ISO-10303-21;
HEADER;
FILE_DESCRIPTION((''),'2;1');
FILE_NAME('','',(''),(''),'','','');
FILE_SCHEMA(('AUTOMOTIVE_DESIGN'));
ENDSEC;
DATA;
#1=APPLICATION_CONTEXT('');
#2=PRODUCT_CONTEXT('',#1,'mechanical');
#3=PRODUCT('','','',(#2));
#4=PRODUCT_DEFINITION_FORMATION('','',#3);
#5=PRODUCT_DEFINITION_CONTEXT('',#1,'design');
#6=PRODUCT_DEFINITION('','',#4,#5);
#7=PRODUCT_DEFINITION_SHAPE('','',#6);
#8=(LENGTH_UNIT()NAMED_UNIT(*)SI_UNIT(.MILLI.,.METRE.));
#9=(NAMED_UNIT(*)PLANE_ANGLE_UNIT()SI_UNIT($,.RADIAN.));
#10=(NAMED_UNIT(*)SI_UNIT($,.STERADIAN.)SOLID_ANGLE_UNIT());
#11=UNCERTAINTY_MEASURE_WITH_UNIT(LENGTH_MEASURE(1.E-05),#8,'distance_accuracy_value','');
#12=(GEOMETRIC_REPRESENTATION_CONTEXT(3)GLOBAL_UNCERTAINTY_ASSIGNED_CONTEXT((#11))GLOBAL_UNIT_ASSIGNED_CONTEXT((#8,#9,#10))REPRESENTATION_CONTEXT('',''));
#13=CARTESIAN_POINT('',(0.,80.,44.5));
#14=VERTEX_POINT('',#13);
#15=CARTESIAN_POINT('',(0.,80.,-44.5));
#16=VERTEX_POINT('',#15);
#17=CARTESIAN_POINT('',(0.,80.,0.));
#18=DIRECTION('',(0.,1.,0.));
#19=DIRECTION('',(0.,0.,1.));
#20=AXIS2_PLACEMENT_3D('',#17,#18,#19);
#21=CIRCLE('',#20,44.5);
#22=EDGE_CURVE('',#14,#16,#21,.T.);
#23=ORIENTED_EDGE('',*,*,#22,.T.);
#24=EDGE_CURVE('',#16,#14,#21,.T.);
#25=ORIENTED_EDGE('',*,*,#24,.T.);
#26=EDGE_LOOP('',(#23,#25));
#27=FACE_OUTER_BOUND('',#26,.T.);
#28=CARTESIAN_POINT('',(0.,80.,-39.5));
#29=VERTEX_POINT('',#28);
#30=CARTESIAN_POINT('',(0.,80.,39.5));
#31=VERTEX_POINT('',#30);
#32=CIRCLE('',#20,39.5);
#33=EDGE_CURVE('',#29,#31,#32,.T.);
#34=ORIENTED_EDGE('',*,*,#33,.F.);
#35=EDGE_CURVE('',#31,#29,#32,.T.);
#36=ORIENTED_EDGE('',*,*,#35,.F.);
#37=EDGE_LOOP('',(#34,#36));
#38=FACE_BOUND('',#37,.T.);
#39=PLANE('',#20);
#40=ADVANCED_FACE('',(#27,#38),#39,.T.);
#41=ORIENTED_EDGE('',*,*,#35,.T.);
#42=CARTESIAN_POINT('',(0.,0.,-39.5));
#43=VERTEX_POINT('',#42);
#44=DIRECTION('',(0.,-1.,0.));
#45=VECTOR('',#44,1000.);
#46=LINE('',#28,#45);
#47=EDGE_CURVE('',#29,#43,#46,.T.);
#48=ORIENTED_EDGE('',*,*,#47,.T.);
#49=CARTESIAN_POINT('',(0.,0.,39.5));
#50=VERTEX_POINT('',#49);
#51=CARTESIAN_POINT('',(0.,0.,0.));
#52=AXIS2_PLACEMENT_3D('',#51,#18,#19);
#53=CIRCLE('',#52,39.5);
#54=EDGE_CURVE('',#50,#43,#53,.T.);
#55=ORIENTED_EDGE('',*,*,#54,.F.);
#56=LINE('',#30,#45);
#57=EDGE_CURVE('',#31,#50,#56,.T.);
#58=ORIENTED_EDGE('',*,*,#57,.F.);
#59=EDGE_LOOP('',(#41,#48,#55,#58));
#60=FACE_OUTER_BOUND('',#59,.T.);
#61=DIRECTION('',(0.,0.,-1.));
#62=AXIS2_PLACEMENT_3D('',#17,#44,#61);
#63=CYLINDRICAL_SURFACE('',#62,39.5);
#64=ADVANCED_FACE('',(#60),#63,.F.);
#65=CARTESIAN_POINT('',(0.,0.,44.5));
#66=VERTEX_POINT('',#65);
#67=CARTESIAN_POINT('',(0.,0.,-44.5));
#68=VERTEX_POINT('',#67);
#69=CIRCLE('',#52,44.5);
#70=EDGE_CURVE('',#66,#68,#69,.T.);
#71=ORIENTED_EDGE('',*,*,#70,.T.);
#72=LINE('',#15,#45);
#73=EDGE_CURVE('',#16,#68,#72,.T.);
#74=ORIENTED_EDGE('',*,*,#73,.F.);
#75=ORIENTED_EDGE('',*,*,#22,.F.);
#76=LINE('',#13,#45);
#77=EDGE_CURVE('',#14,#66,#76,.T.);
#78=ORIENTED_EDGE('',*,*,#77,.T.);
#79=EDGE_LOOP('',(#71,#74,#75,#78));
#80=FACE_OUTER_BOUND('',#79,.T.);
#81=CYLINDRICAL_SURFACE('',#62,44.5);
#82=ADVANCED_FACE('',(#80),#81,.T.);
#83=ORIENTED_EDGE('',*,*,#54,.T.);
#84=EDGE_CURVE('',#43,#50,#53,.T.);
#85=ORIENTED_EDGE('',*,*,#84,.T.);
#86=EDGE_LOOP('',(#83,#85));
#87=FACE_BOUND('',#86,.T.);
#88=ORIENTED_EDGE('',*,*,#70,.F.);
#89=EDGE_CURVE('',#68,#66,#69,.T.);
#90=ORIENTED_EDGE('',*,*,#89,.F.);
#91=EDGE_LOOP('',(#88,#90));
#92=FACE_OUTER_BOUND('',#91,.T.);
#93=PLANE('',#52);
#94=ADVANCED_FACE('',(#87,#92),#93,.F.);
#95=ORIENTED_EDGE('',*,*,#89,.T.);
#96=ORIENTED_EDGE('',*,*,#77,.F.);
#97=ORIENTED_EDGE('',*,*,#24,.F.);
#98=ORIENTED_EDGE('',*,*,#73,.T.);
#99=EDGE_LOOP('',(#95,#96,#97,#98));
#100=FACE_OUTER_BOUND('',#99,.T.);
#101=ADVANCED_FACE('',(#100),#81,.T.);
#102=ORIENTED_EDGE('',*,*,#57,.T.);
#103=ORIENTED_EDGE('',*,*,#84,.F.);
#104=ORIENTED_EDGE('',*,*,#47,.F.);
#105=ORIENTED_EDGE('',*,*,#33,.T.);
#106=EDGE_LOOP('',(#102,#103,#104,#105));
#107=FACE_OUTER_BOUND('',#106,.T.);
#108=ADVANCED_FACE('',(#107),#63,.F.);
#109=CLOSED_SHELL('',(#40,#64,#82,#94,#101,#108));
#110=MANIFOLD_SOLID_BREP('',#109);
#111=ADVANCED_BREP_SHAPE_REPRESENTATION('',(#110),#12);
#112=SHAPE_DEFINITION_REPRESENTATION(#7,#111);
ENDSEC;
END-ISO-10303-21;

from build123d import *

# Parameters (mm, degrees)
SKETCH1_R           = 44.5
SKETCH1_R_2         = 39.5
BOSS_EXTRUDE1_DEPTH = 80


with BuildPart() as part:
    # Sketch1 → Boss-Extrude1 (new body)
    with BuildSketch(Plane(origin=(0, 0, 0), x_dir=(1, 0, 0), z_dir=(0, 1, 0))):
        with Locations(Location((0, 0, 0), (0, 0, 270))):
            Circle(SKETCH1_R)
        with Locations(Location((0, 0, 0), (0, 0, 270))):
            Circle(SKETCH1_R_2, mode=Mode.SUBTRACT)
    extrude(amount=BOSS_EXTRUDE1_DEPTH)


solid = part.part
